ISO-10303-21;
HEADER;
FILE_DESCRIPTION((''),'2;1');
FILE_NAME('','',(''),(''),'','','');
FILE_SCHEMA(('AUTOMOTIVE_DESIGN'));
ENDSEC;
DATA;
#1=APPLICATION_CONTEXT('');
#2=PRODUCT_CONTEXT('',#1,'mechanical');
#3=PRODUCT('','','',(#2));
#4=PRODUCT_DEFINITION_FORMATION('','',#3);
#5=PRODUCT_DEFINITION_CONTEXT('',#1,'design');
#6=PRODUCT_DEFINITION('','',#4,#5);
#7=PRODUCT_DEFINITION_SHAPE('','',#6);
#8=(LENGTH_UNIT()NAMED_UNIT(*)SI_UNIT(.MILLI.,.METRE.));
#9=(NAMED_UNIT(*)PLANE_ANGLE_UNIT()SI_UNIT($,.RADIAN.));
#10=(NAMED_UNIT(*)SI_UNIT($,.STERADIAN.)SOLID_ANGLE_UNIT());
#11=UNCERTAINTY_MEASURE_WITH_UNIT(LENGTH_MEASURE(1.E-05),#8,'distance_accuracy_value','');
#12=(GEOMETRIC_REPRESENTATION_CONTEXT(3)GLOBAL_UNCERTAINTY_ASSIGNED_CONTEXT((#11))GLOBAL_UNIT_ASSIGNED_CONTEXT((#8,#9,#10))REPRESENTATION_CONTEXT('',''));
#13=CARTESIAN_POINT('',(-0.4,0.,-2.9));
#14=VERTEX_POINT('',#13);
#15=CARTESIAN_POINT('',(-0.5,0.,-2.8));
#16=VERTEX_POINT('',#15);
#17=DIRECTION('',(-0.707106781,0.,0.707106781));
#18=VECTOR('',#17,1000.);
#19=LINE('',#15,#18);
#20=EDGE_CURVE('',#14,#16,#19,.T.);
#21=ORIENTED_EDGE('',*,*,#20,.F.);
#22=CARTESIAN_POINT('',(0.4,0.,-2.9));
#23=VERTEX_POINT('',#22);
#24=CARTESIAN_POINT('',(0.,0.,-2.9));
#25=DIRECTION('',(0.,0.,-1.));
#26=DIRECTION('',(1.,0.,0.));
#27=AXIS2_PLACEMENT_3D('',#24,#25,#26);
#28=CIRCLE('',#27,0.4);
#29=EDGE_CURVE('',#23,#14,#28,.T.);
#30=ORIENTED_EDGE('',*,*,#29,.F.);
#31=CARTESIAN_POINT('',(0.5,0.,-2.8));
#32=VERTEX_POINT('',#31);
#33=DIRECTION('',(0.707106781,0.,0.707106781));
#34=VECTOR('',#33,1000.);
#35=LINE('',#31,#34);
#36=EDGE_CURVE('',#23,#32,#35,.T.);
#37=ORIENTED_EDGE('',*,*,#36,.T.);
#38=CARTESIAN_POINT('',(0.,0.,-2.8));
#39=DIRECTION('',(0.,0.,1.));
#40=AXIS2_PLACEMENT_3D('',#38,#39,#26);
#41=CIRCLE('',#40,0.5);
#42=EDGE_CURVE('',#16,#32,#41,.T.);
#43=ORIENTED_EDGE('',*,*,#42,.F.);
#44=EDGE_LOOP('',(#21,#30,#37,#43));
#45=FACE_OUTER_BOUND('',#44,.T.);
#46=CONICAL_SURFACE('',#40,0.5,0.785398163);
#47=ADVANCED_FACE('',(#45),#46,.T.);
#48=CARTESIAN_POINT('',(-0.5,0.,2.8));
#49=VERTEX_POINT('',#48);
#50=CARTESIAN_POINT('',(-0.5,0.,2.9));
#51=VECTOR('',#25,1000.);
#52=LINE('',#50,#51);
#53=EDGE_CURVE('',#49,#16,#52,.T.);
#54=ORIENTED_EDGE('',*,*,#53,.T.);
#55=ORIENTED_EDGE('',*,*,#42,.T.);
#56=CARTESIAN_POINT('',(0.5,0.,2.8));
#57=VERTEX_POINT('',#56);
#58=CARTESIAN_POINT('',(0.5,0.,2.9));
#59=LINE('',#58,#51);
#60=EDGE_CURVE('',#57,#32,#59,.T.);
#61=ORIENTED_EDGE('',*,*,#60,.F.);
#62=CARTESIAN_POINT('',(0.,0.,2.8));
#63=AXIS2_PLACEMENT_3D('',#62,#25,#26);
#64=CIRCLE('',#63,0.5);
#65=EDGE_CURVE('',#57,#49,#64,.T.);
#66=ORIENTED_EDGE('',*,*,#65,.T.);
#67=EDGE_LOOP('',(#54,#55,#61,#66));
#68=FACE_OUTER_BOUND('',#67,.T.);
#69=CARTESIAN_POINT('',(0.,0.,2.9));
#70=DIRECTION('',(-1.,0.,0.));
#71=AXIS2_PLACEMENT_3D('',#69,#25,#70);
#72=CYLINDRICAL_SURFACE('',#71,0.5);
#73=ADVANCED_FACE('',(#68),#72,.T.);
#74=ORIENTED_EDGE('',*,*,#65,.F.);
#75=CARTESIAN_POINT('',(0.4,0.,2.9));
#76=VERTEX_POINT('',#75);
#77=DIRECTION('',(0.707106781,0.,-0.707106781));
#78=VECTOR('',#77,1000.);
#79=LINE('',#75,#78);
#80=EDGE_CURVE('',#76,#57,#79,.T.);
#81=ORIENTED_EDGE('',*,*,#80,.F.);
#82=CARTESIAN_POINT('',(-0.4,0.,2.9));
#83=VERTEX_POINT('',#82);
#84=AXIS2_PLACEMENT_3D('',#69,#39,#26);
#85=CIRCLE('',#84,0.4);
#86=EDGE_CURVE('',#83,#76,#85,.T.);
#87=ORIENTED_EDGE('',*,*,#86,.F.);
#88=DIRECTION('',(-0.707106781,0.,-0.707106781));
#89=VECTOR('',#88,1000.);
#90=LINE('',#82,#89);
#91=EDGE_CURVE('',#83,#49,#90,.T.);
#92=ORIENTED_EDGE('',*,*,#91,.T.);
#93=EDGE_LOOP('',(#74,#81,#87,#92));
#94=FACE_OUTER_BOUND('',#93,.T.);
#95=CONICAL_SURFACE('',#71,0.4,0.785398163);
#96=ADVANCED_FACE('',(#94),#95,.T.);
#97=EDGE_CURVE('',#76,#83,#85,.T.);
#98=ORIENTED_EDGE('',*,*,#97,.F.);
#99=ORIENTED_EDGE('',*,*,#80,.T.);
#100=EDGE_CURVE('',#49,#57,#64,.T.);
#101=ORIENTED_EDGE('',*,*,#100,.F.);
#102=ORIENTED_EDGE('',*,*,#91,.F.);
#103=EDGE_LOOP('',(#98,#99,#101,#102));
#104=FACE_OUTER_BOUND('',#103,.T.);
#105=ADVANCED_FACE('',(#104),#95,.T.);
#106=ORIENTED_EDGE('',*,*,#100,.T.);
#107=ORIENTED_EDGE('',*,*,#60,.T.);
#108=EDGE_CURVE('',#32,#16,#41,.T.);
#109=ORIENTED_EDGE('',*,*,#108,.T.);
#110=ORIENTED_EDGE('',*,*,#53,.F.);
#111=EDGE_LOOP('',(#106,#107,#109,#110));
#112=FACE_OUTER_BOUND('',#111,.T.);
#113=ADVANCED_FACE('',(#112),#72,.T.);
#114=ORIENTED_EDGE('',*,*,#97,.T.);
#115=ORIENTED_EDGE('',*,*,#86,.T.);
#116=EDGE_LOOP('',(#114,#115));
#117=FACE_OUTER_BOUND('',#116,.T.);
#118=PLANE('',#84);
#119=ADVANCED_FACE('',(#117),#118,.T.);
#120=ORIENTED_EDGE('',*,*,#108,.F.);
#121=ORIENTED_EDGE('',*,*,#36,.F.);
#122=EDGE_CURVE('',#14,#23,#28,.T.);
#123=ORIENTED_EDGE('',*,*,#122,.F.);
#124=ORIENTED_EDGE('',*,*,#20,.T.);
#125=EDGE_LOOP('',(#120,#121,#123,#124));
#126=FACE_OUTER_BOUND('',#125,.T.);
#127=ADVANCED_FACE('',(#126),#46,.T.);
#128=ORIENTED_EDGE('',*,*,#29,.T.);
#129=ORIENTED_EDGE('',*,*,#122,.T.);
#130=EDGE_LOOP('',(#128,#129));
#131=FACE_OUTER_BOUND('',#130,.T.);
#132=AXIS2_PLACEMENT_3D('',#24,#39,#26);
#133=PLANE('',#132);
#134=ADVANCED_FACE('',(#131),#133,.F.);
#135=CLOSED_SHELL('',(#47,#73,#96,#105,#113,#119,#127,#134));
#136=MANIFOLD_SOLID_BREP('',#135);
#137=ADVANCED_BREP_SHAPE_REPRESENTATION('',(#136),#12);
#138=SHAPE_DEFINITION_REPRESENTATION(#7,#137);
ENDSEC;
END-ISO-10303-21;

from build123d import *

# Parameters (mm, degrees)
SKETCH1_R           = 0.5
BOSS_EXTRUDE1_DEPTH = 2.9
CHAMFER1_SIZE       = 0.1


with BuildPart() as part:
    # Sketch1 → Boss-Extrude1 (new, symmetric)
    with BuildSketch(Plane.XY):
        Circle(SKETCH1_R)
    extrude(amount=BOSS_EXTRUDE1_DEPTH, both=True)

    # Chamfer1
    chamfer1_edges = [part.edges().sort_by_distance(p)[0] for p in [
        (-0.5, 0, -2.9),
        (-0.5, 0, 2.9),
    ]]
    chamfer(chamfer1_edges, length=CHAMFER1_SIZE)


solid = part.part
